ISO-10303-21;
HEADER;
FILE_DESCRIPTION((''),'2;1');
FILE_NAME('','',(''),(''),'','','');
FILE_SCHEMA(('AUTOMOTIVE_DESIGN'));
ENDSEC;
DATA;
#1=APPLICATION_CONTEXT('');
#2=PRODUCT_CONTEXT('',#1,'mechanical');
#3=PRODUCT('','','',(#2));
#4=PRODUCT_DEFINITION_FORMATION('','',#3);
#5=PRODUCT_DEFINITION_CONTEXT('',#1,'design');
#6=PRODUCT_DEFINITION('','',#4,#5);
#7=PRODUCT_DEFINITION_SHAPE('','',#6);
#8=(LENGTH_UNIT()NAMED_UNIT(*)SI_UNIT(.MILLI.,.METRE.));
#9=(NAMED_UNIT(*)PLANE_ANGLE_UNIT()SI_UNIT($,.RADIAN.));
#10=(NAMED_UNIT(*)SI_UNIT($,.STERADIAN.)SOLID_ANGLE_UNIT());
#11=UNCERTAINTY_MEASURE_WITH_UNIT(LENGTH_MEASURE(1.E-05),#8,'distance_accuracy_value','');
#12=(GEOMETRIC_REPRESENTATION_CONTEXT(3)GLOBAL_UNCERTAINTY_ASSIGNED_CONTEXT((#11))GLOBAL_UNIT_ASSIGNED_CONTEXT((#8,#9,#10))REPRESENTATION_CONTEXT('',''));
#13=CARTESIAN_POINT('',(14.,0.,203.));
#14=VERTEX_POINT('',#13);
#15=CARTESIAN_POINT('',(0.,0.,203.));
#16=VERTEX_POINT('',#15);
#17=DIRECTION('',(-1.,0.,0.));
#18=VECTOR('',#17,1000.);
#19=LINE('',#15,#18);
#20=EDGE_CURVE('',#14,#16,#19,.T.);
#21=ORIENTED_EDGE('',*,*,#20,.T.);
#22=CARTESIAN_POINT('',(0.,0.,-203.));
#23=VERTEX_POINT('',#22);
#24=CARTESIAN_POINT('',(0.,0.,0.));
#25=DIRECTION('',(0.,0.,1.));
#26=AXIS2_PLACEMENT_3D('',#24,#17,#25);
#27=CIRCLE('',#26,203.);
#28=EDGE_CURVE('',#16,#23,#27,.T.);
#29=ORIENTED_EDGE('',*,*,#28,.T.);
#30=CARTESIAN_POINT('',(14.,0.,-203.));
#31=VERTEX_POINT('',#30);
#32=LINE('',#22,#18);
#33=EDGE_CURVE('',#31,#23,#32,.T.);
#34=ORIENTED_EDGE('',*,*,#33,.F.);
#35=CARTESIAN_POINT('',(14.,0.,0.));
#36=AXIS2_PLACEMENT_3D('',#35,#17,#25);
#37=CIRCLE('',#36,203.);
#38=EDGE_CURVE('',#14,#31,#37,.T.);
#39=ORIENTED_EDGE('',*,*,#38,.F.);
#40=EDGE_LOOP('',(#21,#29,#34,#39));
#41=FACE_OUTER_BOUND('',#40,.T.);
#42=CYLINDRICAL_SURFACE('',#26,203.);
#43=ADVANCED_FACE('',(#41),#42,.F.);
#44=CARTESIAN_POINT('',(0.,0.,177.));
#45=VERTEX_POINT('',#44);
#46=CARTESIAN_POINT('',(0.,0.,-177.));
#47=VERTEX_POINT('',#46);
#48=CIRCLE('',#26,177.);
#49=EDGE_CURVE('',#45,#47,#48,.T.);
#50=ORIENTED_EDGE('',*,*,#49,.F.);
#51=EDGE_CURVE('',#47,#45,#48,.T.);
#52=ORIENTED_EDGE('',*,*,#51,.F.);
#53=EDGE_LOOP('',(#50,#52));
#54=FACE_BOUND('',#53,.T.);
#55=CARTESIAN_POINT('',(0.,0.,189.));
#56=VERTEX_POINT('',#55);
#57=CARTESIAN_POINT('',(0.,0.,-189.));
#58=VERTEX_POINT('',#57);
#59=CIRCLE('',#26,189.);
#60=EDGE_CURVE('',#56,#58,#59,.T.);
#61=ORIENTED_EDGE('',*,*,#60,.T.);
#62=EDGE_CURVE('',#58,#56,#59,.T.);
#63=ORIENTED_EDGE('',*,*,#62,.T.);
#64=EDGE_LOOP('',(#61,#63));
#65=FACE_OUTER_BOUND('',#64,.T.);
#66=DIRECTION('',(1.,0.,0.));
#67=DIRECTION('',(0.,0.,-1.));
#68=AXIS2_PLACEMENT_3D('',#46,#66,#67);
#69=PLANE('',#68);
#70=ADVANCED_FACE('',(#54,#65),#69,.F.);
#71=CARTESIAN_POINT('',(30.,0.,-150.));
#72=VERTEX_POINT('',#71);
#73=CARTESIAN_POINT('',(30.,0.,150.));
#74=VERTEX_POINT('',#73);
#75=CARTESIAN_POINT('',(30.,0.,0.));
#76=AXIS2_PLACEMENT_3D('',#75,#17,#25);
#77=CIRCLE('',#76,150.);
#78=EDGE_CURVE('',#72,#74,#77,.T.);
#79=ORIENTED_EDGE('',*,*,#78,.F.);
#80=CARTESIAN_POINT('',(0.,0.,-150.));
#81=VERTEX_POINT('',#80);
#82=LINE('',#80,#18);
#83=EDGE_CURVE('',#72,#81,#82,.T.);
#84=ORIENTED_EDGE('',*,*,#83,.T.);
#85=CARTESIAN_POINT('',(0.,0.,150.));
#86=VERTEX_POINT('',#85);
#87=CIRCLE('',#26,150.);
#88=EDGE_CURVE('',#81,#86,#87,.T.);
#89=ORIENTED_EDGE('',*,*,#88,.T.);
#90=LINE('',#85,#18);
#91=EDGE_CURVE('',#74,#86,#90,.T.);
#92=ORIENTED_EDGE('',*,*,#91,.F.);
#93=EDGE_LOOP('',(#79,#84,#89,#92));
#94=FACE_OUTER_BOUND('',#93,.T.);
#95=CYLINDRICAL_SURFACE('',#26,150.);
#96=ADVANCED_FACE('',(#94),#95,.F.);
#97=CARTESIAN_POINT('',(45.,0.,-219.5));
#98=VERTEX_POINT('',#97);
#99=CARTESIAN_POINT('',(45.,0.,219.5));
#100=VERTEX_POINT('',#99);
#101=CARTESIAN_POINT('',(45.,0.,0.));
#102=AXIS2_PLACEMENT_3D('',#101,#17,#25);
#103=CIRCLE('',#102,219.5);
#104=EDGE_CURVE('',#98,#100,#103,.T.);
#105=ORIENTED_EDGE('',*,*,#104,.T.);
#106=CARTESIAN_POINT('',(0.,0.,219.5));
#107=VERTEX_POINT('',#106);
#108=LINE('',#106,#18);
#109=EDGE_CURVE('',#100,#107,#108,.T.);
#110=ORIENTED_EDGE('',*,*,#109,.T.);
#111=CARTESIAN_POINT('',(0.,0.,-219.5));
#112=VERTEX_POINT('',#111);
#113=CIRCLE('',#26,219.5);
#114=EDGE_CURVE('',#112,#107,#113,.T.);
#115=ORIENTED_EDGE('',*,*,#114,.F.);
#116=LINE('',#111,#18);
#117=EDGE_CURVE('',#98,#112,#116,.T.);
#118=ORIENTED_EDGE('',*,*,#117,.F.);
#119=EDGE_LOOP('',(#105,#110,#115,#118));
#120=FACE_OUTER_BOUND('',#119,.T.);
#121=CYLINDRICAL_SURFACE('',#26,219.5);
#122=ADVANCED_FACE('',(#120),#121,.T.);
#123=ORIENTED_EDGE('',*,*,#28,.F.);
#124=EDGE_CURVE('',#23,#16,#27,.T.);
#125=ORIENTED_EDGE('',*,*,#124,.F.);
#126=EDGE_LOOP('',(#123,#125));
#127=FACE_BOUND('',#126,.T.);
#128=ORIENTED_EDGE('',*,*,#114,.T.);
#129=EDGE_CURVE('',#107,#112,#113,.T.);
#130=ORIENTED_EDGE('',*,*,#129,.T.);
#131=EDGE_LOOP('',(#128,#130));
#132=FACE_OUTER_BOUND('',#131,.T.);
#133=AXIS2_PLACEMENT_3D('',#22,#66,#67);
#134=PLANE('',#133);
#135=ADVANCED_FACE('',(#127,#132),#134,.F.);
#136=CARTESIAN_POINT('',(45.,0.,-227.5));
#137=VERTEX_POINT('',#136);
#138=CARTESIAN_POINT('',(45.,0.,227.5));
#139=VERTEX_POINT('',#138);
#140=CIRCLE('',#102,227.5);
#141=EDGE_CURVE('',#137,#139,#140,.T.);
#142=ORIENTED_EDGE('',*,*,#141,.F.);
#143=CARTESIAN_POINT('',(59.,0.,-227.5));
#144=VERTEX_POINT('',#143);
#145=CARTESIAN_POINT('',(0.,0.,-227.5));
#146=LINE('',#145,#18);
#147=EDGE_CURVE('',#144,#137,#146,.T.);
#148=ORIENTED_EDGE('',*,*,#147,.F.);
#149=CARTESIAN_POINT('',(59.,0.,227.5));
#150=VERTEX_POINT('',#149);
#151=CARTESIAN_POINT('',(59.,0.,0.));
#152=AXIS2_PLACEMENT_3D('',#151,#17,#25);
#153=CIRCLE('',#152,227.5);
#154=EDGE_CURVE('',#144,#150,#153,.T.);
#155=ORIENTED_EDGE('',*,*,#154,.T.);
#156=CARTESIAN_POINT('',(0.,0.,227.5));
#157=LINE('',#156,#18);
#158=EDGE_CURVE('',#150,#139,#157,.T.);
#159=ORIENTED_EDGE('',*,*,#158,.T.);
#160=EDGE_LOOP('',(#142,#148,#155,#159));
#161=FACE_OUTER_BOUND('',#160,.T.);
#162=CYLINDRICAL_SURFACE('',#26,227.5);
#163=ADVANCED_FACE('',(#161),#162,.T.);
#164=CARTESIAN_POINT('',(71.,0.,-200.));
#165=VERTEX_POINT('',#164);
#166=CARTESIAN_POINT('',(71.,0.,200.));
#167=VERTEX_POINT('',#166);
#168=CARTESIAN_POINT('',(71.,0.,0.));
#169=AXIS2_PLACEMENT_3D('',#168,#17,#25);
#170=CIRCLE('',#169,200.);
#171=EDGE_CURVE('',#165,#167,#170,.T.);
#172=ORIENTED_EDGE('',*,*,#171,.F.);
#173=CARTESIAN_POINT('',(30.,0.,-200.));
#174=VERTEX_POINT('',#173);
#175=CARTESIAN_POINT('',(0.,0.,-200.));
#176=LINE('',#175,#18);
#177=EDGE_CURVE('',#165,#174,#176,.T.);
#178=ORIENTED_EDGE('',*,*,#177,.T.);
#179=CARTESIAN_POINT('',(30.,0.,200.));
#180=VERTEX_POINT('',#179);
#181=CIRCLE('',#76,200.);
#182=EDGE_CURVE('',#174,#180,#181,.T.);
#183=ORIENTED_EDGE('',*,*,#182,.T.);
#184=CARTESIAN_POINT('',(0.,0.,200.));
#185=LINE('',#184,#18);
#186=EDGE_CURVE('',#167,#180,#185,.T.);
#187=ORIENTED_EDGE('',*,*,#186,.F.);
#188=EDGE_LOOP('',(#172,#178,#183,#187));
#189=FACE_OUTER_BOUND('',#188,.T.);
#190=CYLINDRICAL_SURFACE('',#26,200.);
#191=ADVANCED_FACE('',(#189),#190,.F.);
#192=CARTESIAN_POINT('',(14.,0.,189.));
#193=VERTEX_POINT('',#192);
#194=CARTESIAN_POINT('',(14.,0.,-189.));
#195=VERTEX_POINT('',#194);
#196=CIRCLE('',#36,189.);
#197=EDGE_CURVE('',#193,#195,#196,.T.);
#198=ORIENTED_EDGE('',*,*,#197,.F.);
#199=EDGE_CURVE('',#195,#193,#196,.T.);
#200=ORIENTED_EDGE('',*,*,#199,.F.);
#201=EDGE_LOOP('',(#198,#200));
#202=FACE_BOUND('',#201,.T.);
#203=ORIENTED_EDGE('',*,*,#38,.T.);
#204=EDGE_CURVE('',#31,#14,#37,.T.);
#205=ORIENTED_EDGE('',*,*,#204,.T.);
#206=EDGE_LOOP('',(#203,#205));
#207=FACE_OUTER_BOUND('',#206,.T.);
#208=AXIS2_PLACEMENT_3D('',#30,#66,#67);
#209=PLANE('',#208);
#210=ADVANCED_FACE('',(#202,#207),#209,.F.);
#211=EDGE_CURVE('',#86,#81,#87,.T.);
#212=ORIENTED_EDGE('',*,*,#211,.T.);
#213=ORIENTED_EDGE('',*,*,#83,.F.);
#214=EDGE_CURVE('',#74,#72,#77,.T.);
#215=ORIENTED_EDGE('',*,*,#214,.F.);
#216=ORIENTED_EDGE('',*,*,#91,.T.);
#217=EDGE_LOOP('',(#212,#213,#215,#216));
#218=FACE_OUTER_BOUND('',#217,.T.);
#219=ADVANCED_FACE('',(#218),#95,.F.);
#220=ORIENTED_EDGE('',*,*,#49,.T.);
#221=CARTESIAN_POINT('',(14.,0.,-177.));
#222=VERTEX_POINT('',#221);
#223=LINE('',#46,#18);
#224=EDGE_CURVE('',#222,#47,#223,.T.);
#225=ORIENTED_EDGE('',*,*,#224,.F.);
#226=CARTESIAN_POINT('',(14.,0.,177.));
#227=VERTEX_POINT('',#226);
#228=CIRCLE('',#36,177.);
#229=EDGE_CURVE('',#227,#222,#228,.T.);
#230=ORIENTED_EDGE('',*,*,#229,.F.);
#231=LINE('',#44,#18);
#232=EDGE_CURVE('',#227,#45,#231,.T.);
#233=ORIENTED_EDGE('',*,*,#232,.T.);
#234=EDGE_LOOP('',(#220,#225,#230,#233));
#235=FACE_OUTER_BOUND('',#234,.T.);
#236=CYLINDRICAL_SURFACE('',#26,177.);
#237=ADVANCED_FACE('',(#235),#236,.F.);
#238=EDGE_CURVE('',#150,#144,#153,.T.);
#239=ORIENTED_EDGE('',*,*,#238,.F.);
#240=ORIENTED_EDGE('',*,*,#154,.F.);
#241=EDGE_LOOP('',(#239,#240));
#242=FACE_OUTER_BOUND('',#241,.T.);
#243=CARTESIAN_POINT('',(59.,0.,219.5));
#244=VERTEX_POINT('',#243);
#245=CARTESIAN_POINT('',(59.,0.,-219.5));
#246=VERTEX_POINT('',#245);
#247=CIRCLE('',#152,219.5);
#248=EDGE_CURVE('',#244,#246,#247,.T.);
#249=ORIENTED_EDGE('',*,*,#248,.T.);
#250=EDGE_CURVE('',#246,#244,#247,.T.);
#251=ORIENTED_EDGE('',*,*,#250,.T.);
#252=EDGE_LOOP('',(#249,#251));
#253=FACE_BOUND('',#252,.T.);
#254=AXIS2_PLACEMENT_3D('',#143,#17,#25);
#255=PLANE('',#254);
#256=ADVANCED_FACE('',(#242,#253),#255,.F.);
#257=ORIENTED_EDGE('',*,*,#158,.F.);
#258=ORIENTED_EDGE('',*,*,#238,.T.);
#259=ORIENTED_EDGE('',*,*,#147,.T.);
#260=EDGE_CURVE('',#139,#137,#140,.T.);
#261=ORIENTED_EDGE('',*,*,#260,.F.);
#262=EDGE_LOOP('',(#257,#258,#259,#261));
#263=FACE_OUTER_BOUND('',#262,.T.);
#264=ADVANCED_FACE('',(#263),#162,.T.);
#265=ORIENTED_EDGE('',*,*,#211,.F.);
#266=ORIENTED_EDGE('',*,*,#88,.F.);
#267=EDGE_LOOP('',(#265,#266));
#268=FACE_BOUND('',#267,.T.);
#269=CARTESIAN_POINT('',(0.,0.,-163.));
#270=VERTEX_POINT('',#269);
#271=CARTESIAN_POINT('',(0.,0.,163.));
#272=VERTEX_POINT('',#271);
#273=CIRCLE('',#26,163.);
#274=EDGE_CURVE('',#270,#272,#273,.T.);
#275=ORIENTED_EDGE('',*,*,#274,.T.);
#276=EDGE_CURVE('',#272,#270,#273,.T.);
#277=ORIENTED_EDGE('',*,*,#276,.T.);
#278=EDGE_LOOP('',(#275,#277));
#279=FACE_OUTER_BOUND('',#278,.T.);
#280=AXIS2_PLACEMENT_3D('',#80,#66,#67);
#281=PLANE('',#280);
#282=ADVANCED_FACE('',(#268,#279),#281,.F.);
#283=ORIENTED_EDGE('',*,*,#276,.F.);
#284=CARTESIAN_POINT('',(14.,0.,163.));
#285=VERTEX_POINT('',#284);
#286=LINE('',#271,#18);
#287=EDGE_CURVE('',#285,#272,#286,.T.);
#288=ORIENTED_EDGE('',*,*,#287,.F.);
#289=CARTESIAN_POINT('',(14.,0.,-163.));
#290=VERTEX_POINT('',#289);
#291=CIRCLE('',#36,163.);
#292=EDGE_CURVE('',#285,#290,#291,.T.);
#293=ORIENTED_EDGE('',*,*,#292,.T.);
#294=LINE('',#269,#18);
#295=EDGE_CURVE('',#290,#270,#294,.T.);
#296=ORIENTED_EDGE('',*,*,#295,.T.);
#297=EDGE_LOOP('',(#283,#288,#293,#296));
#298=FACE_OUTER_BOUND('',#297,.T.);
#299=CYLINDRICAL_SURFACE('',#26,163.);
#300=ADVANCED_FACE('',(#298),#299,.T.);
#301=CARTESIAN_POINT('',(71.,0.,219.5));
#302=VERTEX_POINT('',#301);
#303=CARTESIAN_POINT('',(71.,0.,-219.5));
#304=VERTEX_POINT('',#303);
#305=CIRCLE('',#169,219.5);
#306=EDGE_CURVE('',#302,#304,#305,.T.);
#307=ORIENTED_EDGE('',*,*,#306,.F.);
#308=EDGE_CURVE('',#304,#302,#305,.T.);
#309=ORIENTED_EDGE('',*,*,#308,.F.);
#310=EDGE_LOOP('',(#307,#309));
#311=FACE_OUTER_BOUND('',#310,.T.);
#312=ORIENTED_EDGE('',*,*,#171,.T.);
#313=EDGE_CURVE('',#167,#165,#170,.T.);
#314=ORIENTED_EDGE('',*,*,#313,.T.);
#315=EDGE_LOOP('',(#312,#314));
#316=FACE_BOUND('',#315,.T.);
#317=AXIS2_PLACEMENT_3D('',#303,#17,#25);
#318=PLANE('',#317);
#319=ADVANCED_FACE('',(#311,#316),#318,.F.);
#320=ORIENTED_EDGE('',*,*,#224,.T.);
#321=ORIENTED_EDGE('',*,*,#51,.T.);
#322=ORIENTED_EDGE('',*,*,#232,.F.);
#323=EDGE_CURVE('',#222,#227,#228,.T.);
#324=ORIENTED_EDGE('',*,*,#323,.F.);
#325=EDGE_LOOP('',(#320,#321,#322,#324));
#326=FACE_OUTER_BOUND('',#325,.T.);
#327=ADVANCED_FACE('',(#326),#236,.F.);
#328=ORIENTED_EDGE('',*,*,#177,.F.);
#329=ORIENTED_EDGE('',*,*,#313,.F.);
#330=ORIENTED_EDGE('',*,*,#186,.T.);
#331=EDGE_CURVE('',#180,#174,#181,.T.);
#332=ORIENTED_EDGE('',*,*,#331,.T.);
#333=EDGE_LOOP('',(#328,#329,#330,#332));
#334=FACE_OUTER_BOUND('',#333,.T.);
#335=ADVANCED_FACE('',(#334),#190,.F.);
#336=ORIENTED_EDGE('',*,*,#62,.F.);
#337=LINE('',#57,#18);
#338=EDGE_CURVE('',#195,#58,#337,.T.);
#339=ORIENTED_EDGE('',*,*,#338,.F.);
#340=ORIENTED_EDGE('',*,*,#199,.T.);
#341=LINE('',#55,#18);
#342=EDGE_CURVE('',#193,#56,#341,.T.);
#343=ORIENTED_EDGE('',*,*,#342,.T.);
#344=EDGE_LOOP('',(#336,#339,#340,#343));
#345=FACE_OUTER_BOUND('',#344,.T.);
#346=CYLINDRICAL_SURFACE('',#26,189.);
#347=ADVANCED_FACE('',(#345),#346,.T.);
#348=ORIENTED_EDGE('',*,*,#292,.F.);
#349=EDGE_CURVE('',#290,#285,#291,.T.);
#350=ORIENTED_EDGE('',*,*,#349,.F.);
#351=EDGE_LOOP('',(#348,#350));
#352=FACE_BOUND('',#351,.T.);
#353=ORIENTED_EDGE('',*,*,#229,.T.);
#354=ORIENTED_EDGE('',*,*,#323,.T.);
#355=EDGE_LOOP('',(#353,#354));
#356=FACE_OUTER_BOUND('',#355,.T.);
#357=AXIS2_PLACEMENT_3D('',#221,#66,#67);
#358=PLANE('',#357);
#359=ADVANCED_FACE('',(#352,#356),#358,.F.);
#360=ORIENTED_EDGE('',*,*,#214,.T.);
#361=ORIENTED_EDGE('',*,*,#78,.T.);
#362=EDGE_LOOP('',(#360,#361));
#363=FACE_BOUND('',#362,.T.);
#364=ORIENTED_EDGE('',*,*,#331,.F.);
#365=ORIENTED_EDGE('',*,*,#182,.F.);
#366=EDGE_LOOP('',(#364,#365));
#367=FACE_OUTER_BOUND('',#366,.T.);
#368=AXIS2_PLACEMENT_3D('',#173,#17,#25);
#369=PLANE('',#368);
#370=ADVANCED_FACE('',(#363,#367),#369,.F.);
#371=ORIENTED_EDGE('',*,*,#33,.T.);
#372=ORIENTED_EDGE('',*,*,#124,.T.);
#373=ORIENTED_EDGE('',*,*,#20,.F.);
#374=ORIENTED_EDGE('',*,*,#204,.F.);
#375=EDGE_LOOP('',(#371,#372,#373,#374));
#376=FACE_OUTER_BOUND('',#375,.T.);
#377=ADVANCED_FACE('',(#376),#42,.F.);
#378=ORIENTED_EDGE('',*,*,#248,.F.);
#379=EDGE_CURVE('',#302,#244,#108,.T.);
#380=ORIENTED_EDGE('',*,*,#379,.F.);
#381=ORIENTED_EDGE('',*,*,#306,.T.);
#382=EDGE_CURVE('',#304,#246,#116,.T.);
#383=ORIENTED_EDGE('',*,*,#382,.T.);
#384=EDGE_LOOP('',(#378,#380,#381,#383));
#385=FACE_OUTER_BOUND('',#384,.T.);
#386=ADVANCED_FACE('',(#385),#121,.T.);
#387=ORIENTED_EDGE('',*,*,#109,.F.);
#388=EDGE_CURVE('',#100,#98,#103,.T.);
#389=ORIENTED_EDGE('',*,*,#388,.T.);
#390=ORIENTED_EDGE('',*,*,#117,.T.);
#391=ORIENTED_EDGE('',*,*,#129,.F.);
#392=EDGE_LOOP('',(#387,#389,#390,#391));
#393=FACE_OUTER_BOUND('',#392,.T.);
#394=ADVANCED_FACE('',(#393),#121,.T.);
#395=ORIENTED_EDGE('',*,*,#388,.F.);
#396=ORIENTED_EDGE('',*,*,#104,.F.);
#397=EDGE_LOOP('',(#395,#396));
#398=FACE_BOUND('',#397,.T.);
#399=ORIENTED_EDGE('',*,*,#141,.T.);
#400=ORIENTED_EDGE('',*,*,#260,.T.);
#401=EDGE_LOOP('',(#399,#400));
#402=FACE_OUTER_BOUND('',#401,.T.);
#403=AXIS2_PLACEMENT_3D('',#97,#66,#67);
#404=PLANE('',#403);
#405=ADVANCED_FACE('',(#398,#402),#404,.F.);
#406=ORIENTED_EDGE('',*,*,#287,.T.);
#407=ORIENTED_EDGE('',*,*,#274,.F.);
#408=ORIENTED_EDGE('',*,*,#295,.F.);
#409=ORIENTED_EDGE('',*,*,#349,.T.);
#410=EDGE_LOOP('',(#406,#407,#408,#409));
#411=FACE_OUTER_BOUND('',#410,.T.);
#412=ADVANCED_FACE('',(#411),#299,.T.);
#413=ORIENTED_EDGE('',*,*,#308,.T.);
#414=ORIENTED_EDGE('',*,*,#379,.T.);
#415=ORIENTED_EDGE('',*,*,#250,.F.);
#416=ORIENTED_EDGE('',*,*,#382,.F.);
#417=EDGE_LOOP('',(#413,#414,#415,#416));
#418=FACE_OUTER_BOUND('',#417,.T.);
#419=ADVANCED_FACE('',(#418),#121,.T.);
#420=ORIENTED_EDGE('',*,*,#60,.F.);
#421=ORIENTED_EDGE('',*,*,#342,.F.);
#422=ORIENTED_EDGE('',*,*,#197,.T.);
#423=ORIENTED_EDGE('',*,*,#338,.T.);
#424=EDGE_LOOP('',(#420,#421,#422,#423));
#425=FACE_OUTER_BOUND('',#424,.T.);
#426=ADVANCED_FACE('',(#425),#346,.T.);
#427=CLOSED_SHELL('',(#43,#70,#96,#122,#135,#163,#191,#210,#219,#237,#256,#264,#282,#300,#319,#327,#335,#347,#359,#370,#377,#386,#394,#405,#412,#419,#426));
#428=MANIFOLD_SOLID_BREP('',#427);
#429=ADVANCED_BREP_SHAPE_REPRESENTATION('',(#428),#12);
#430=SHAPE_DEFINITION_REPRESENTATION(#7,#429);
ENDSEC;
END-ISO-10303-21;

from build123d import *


with BuildPart() as part:
    # Sketch1 → Revolve1 (revolve)
    with BuildSketch(Plane(origin=(0, 0, 0), x_dir=(1, 0, 0), z_dir=(0, 1, 0)), mode=Mode.PRIVATE) as revolve1_sk:
        Polygon((0, 150), (0, 163), (14, 163), (14, 177), (0, 177), (0, 189), (14, 189), (14, 203), (0, 203), (0, 219.5), (45, 219.5), (45, 227.5), (59, 227.5), (59, 219.5), (71, 219.5), (71, 200), (30, 200), (30, 150), align=None)
    revolve(revolve1_sk.sketch.rotate(Axis((0, 0, 0), (1, 0, 0)), 180), axis=Axis((0, 0, 0), (1, 0, 0)))


solid = part.part
